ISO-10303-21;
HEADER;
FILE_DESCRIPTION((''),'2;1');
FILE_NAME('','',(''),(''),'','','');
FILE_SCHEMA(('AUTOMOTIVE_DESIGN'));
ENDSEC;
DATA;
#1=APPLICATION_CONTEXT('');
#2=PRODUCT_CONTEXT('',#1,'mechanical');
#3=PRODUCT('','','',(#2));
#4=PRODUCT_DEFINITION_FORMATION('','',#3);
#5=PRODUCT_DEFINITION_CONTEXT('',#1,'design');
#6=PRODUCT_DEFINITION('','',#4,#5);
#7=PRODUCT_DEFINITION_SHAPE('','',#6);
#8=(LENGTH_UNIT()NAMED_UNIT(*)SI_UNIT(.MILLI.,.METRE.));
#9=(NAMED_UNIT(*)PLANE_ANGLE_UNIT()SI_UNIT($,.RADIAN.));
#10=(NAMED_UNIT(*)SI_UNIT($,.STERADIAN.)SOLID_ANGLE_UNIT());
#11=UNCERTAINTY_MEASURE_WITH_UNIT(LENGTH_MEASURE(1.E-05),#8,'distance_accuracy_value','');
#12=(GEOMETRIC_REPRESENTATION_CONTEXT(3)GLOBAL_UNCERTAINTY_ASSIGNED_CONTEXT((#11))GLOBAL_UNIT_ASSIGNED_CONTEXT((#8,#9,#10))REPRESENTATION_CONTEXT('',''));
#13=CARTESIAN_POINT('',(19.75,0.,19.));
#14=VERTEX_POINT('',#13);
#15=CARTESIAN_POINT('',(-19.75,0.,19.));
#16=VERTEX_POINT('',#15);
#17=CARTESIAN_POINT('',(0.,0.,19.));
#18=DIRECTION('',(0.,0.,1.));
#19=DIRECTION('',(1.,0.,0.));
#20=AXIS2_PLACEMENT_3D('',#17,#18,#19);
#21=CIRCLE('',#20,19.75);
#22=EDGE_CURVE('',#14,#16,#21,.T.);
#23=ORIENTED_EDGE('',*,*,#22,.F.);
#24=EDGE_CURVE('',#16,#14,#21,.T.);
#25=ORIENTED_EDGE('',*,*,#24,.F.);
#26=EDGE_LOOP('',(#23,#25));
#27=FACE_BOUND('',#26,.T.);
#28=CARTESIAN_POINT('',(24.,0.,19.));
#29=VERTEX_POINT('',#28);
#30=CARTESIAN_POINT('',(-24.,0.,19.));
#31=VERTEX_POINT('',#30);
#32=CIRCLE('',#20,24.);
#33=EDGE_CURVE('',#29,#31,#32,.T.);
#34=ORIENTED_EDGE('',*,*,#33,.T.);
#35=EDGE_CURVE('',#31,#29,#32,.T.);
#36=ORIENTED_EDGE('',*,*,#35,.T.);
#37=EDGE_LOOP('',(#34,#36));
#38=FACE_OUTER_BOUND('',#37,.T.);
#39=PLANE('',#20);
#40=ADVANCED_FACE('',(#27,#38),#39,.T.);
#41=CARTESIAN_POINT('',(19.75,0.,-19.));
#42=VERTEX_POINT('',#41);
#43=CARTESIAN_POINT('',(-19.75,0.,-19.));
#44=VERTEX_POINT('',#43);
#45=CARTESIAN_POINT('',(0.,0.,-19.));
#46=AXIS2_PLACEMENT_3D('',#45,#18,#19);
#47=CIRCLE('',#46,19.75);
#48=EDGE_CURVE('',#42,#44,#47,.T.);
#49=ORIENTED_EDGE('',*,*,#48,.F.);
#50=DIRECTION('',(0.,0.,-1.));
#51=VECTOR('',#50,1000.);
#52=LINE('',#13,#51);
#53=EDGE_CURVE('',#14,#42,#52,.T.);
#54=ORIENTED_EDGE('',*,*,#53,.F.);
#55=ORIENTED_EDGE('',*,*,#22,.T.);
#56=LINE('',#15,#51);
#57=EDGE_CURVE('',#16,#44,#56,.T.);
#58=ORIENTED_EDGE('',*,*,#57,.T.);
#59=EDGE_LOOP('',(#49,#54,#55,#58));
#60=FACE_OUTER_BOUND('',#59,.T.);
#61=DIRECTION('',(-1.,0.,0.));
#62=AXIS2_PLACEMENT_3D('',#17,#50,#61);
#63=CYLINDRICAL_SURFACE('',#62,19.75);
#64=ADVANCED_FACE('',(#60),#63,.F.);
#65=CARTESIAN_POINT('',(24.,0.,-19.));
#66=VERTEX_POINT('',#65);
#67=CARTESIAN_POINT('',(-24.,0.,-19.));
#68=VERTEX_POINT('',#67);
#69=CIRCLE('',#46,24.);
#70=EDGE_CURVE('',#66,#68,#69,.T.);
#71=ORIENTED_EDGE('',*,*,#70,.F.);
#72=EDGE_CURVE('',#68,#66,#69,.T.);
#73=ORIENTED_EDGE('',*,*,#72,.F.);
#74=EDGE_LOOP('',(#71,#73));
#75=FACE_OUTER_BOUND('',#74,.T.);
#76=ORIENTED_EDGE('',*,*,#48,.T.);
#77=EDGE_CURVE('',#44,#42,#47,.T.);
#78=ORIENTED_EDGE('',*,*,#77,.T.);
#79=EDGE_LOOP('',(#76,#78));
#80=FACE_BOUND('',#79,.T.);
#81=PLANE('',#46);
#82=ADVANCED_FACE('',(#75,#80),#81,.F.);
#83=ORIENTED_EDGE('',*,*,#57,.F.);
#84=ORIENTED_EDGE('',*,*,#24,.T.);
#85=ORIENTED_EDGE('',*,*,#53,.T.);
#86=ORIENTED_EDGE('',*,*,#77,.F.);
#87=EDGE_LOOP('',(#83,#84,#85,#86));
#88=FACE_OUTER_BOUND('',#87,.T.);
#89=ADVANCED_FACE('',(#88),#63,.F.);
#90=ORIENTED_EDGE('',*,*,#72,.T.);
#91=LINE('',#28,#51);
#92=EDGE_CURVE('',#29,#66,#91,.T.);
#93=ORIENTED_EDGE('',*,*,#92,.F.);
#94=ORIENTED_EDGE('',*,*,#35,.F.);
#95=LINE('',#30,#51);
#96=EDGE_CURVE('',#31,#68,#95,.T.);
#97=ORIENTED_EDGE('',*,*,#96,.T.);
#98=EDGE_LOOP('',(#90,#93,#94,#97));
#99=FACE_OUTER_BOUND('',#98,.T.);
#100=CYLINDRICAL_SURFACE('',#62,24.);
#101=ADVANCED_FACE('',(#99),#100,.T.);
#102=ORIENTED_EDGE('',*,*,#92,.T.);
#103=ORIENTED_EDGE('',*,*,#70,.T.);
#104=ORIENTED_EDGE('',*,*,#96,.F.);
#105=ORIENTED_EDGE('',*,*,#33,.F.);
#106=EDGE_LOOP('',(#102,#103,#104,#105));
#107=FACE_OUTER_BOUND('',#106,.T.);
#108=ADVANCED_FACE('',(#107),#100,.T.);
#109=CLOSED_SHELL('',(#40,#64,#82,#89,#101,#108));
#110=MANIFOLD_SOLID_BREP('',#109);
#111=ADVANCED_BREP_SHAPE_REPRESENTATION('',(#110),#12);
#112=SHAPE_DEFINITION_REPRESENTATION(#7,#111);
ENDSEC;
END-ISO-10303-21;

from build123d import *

# Parameters (mm, degrees)
SKETCH1_R           = 24
SKETCH1_R_2         = 19.75
BOSS_EXTRUDE1_DEPTH = 19


with BuildPart() as part:
    # Sketch1 → Boss-Extrude1 (new, symmetric)
    with BuildSketch(Plane.XY):
        Circle(SKETCH1_R)
        Circle(SKETCH1_R_2, mode=Mode.SUBTRACT)
    extrude(amount=BOSS_EXTRUDE1_DEPTH, both=True)


solid = part.part
